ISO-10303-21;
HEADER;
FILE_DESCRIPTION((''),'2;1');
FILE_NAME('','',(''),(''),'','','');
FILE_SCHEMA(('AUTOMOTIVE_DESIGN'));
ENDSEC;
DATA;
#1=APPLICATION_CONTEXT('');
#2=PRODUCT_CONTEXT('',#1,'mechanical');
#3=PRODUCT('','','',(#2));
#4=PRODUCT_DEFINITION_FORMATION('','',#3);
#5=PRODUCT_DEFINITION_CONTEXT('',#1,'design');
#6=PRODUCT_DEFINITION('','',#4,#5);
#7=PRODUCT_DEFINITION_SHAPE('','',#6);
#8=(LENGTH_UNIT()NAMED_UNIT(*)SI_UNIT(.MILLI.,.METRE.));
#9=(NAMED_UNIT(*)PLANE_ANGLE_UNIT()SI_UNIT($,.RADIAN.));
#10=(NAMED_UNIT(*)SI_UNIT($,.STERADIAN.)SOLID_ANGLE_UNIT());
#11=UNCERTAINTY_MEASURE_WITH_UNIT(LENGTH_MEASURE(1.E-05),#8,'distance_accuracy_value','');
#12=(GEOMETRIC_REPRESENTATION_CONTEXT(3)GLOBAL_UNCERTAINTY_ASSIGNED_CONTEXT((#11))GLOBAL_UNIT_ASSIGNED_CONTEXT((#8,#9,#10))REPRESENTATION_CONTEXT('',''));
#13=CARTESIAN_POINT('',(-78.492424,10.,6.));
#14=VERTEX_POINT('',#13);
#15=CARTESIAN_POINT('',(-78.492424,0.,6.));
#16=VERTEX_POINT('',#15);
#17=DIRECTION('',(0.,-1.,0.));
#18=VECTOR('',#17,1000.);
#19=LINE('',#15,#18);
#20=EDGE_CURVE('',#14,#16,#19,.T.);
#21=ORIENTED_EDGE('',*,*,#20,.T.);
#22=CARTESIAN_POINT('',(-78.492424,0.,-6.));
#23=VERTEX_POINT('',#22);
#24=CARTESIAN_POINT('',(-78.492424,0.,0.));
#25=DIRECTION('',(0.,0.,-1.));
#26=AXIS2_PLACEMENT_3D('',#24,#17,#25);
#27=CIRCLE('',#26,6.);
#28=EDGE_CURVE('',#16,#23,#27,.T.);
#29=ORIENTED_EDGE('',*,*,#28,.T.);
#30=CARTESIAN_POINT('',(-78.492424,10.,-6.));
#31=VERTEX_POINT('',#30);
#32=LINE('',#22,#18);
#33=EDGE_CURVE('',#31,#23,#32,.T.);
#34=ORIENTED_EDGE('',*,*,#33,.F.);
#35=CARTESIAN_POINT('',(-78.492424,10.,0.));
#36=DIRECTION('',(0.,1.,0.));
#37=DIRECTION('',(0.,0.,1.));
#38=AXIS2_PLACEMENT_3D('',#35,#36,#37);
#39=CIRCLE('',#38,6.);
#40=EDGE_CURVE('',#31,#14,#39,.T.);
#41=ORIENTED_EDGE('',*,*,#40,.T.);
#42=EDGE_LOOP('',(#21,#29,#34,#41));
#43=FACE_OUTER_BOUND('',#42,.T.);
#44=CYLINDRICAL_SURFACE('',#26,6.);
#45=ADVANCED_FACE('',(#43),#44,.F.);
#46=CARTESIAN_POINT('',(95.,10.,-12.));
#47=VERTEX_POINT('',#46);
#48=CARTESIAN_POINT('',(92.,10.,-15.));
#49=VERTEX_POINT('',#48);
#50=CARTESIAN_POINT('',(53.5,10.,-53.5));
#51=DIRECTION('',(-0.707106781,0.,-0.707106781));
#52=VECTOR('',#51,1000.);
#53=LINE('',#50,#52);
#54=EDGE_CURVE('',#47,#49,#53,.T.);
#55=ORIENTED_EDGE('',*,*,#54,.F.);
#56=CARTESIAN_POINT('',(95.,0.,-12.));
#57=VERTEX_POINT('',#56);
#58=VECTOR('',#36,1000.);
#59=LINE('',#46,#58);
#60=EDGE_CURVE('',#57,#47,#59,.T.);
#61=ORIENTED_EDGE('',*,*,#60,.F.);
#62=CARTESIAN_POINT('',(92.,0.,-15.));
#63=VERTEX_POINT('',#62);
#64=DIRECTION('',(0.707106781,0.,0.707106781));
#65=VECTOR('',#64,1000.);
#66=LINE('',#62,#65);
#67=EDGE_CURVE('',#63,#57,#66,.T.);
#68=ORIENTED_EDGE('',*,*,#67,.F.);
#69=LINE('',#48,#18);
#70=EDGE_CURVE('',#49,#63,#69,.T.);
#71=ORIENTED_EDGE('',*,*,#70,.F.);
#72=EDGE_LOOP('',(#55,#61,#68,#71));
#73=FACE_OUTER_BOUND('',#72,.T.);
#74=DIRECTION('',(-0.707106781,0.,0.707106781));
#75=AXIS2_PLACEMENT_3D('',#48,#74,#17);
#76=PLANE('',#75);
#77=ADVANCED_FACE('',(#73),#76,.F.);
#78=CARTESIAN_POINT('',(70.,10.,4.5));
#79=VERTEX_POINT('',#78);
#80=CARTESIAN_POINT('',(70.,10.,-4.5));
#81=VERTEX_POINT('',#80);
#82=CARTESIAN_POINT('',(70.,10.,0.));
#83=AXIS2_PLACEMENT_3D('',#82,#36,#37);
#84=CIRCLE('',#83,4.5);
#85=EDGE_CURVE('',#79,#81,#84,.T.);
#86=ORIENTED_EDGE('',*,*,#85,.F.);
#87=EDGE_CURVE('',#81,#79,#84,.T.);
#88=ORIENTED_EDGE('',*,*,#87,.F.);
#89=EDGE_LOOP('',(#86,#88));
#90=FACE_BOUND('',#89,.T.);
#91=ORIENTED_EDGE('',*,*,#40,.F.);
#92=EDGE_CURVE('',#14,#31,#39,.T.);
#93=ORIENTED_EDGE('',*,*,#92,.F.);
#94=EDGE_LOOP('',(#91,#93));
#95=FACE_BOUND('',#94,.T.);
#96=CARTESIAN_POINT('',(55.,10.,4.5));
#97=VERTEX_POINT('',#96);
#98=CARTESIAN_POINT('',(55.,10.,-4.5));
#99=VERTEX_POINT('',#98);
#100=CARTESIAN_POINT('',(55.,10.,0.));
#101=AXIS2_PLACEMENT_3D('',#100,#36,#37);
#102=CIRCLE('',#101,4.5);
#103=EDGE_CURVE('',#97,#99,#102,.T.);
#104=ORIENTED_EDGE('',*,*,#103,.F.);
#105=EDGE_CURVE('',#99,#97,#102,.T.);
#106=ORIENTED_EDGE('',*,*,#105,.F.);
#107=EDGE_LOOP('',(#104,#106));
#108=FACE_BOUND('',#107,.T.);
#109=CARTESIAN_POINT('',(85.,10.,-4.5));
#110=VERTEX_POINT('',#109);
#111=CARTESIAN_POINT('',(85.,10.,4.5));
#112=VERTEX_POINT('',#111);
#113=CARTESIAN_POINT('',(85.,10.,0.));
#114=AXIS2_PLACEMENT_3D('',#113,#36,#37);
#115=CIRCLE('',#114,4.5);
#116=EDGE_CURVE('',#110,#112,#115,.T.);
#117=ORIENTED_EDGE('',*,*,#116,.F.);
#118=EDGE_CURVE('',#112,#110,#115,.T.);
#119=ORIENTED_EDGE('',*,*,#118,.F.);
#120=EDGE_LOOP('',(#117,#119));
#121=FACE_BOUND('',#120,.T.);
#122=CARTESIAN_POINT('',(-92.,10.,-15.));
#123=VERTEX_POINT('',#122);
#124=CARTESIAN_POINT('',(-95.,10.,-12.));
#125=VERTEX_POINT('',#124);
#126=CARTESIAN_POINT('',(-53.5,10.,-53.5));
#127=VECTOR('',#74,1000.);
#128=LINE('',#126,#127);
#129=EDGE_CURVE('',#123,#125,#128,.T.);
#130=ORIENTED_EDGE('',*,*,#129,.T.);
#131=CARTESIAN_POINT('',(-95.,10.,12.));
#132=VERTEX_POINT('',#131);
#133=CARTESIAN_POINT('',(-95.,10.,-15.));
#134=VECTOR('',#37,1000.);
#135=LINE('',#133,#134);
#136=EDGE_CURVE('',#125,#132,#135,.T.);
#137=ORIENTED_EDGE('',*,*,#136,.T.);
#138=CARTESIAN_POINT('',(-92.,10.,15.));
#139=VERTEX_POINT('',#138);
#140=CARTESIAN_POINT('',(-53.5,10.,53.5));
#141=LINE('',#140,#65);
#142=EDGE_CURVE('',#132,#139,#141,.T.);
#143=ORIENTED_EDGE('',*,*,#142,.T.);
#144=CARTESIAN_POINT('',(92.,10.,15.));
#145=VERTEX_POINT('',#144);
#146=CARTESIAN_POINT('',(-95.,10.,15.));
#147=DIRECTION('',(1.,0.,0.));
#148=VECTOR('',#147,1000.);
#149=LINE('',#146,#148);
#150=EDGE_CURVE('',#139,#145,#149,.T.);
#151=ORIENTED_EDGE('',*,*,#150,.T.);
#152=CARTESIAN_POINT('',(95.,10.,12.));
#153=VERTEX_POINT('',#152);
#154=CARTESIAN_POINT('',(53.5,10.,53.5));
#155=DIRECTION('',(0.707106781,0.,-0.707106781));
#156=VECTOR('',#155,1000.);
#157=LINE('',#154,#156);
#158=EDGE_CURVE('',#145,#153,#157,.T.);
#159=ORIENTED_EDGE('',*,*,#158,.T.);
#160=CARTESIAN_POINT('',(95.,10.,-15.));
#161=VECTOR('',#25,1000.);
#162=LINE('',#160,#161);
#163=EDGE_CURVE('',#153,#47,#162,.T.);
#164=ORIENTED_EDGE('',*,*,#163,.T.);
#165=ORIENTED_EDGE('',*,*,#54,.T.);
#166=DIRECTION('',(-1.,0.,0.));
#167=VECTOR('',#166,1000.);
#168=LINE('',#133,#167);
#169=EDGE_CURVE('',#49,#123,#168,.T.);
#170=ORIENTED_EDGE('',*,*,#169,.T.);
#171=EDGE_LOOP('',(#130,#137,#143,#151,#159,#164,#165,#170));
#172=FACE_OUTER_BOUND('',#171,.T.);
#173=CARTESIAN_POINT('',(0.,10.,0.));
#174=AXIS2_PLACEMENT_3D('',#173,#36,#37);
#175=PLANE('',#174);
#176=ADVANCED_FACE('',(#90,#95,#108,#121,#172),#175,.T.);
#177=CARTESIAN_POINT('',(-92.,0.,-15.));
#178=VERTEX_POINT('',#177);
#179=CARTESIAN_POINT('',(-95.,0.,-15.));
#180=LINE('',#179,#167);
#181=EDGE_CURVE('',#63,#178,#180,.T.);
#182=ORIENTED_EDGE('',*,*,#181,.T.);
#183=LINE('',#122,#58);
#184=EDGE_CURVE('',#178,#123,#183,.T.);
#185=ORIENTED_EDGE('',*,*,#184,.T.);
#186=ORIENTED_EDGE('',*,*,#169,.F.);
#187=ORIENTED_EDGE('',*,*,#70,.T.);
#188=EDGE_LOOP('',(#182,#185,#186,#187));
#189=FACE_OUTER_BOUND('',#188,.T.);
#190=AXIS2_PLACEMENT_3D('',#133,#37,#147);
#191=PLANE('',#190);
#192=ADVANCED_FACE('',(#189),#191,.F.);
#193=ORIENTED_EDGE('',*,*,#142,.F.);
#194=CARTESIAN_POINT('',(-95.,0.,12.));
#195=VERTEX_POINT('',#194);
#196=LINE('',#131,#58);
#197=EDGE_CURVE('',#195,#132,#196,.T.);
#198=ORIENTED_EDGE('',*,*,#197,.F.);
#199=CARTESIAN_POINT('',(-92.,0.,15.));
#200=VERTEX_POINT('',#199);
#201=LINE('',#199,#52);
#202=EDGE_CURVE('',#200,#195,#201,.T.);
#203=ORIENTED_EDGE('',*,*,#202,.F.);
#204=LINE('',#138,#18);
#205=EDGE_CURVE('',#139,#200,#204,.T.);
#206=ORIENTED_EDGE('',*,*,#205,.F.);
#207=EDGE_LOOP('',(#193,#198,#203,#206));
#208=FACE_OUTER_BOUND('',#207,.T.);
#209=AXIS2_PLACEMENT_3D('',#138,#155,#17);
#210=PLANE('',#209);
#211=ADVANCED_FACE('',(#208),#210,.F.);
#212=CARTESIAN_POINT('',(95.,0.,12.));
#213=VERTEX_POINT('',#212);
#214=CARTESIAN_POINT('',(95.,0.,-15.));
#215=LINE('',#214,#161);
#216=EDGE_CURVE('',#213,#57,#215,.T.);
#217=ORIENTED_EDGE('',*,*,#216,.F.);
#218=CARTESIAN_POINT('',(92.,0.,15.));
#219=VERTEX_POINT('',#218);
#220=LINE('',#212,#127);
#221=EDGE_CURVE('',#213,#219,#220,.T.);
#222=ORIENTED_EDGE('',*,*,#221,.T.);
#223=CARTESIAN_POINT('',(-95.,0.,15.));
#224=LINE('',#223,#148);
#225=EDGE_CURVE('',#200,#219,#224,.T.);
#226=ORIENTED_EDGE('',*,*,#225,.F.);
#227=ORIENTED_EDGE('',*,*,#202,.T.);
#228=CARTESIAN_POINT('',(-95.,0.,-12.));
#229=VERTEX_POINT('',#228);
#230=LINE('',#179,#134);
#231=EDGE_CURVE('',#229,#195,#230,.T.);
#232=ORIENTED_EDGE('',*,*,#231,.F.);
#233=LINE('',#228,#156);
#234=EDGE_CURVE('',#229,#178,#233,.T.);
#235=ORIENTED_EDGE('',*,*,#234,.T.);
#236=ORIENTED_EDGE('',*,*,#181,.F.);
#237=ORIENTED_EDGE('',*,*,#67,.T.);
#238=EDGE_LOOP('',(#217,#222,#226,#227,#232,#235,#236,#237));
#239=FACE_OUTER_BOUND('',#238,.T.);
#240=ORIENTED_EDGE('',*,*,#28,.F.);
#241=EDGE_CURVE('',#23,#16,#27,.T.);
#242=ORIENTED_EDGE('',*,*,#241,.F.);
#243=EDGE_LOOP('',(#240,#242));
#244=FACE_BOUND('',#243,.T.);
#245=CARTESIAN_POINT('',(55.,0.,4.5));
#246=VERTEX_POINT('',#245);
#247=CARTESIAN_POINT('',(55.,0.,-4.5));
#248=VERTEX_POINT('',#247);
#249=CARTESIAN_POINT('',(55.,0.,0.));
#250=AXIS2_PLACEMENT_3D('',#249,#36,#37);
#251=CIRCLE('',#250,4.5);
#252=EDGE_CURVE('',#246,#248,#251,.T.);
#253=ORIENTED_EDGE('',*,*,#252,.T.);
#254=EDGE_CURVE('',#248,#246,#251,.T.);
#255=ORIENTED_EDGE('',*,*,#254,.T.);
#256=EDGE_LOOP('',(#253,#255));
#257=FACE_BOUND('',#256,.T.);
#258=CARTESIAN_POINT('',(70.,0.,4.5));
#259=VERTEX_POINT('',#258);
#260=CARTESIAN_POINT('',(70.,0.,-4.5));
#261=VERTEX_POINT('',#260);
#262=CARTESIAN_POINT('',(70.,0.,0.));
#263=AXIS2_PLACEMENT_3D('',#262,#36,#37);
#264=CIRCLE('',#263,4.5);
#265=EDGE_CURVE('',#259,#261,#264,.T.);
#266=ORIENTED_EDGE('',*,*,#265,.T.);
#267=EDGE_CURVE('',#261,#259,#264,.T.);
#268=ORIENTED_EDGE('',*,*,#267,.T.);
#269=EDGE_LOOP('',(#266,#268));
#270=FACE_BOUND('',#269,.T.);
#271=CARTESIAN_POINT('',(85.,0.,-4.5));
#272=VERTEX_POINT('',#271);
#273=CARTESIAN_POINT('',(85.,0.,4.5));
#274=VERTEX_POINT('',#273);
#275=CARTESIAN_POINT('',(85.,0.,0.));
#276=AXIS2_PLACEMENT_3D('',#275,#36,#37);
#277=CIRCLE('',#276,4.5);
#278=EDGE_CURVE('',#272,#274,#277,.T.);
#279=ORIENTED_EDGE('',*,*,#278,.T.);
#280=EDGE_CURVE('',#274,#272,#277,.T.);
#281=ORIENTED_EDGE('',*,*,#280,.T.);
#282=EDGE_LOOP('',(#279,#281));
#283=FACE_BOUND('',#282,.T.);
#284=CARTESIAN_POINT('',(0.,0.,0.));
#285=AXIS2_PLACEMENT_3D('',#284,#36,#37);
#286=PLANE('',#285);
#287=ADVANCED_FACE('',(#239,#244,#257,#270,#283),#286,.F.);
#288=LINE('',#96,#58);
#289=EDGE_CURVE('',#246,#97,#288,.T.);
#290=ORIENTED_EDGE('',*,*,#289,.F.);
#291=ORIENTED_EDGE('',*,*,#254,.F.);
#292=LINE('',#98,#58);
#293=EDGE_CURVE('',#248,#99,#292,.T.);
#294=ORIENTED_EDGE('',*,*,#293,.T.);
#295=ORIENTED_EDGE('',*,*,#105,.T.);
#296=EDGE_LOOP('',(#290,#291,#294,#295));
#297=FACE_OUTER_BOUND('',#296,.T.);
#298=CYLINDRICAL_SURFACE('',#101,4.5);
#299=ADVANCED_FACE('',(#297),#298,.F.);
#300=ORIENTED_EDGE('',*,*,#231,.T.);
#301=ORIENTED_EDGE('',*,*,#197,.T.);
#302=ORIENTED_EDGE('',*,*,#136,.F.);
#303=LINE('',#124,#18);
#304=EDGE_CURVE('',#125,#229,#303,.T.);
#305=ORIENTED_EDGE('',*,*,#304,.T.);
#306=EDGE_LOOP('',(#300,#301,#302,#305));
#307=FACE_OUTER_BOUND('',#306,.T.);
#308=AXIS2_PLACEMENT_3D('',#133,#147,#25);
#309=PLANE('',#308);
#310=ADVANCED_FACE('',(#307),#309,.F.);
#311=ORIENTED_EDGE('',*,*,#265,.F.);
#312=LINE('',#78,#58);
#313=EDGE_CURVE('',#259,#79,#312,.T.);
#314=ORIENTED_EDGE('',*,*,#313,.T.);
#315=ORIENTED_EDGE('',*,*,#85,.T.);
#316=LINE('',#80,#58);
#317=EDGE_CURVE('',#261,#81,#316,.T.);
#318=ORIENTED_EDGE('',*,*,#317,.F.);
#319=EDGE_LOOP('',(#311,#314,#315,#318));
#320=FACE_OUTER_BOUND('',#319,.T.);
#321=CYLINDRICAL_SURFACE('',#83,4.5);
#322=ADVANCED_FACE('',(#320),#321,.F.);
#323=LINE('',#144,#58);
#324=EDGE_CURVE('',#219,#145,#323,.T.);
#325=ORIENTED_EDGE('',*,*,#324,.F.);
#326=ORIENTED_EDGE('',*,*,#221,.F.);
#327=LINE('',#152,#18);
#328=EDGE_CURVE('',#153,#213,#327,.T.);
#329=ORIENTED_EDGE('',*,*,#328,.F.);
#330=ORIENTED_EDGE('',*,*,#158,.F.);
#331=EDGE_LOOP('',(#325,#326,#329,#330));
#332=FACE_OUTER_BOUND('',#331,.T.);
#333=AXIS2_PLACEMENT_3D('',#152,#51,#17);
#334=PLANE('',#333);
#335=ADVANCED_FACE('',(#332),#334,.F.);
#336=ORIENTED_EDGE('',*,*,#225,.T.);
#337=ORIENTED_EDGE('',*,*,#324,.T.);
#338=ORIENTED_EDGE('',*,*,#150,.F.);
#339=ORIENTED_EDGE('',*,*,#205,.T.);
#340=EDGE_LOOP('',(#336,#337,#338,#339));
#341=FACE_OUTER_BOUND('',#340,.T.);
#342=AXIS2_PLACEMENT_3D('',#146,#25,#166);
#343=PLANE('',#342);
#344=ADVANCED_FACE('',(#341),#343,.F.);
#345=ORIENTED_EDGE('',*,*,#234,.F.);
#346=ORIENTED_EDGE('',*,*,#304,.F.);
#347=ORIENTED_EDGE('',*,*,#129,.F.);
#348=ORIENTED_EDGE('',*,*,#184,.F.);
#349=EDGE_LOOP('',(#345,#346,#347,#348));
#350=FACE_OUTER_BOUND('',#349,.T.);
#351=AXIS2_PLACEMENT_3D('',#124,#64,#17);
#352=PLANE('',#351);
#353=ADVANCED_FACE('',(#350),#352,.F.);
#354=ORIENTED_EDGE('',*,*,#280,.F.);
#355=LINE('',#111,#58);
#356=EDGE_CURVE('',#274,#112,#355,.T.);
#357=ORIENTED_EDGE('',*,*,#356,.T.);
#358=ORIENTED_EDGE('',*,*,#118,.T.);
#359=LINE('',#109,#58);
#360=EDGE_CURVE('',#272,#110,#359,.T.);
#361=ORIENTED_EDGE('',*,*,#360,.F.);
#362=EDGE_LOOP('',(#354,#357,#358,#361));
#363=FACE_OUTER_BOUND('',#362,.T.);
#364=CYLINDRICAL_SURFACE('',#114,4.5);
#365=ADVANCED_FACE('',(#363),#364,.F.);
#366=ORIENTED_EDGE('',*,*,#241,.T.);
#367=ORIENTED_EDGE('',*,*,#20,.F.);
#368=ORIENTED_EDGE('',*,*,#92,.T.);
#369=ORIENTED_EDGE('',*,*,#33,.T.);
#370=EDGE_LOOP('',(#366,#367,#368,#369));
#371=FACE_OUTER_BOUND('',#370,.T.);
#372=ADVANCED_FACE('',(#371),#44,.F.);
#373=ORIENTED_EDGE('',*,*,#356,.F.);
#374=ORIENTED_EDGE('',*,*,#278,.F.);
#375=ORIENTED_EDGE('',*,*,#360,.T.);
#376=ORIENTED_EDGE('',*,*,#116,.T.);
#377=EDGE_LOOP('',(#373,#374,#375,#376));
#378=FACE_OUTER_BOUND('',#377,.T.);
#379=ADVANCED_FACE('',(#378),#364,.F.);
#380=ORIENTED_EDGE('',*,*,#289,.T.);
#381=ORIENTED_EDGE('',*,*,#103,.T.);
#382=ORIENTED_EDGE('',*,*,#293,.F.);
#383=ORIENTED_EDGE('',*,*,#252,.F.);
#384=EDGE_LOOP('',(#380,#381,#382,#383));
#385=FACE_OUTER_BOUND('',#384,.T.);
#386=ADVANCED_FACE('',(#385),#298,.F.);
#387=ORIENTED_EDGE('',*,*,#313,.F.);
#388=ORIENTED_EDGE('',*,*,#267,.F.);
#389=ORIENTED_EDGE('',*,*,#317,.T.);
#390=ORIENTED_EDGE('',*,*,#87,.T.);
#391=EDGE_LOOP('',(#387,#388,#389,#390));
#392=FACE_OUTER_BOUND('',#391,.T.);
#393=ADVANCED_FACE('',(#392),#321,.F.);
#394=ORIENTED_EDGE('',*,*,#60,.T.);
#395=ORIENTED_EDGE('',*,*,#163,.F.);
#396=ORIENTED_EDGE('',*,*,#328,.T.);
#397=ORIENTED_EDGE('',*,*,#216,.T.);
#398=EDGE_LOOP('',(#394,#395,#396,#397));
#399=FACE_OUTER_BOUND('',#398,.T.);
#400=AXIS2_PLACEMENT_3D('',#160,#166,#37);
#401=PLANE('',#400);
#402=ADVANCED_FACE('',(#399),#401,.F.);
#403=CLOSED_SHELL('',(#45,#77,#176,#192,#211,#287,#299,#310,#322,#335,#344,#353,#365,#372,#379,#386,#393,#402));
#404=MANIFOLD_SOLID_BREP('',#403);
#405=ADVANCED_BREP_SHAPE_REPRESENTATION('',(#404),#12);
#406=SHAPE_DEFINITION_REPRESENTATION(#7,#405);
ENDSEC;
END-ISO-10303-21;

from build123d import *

# Parameters (mm, degrees)
SKETCH1_W                    = 190
SKETCH1_H                    = 30
BOSS_EXTRUDE1_DEPTH          = 10
CHAMFER1_SIZE                = 3
F_9_0_9_DIAMETER_HOLE1_D     = 9
F_9_0_9_DIAMETER_HOLE1_DEPTH = 19.75
F_9_0_9_DIAMETER_HOLE1_TIP   = 2.703872786
F_9_0_9_DIAMETER_HOLE2_D     = 12
F_9_0_9_DIAMETER_HOLE2_DEPTH = 19.75
F_9_0_9_DIAMETER_HOLE2_TIP   = 3.605163714


with BuildPart() as part:
    # Sketch1 → Boss-Extrude1 (new body)
    with BuildSketch(Plane(origin=(0, 0, 0), x_dir=(1, 0, 0), z_dir=(0, 1, 0))):
        Rectangle(SKETCH1_W, SKETCH1_H)
    extrude(amount=BOSS_EXTRUDE1_DEPTH)

    # Chamfer1
    chamfer1_edges = [part.edges().sort_by_distance(p)[0] for p in [
        (95, 5, 15),
        (-95, 5, 15),
        (-95, 5, -15),
        (95, 5, -15),
    ]]
    chamfer(chamfer1_edges, length=CHAMFER1_SIZE)

    # Ø9.0 (9) Diameter Hole1
    with Locations(Plane(origin=(0, 10, 0), x_dir=(1, 0, 0), z_dir=(0, 1, 0))):
        with Locations((85, 0), (70, 0), (55, 0)):
            Hole(F_9_0_9_DIAMETER_HOLE1_D / 2, depth=F_9_0_9_DIAMETER_HOLE1_DEPTH)
            with Locations((0, 0, -(F_9_0_9_DIAMETER_HOLE1_DEPTH + F_9_0_9_DIAMETER_HOLE1_TIP / 2))):  # 118° drill point
                Cone(0, F_9_0_9_DIAMETER_HOLE1_D / 2, F_9_0_9_DIAMETER_HOLE1_TIP, mode=Mode.SUBTRACT)

    # Ø9.0 (9) Diameter Hole2
    with Locations(Plane(origin=(0, 0, 0), x_dir=(-1, 0, 0), z_dir=(0, -1, 0))):
        with Locations((78.492424049, 0)):
            Hole(F_9_0_9_DIAMETER_HOLE2_D / 2, depth=F_9_0_9_DIAMETER_HOLE2_DEPTH)
            with Locations((0, 0, -(F_9_0_9_DIAMETER_HOLE2_DEPTH + F_9_0_9_DIAMETER_HOLE2_TIP / 2))):  # 118° drill point
                Cone(0, F_9_0_9_DIAMETER_HOLE2_D / 2, F_9_0_9_DIAMETER_HOLE2_TIP, mode=Mode.SUBTRACT)


solid = part.part
